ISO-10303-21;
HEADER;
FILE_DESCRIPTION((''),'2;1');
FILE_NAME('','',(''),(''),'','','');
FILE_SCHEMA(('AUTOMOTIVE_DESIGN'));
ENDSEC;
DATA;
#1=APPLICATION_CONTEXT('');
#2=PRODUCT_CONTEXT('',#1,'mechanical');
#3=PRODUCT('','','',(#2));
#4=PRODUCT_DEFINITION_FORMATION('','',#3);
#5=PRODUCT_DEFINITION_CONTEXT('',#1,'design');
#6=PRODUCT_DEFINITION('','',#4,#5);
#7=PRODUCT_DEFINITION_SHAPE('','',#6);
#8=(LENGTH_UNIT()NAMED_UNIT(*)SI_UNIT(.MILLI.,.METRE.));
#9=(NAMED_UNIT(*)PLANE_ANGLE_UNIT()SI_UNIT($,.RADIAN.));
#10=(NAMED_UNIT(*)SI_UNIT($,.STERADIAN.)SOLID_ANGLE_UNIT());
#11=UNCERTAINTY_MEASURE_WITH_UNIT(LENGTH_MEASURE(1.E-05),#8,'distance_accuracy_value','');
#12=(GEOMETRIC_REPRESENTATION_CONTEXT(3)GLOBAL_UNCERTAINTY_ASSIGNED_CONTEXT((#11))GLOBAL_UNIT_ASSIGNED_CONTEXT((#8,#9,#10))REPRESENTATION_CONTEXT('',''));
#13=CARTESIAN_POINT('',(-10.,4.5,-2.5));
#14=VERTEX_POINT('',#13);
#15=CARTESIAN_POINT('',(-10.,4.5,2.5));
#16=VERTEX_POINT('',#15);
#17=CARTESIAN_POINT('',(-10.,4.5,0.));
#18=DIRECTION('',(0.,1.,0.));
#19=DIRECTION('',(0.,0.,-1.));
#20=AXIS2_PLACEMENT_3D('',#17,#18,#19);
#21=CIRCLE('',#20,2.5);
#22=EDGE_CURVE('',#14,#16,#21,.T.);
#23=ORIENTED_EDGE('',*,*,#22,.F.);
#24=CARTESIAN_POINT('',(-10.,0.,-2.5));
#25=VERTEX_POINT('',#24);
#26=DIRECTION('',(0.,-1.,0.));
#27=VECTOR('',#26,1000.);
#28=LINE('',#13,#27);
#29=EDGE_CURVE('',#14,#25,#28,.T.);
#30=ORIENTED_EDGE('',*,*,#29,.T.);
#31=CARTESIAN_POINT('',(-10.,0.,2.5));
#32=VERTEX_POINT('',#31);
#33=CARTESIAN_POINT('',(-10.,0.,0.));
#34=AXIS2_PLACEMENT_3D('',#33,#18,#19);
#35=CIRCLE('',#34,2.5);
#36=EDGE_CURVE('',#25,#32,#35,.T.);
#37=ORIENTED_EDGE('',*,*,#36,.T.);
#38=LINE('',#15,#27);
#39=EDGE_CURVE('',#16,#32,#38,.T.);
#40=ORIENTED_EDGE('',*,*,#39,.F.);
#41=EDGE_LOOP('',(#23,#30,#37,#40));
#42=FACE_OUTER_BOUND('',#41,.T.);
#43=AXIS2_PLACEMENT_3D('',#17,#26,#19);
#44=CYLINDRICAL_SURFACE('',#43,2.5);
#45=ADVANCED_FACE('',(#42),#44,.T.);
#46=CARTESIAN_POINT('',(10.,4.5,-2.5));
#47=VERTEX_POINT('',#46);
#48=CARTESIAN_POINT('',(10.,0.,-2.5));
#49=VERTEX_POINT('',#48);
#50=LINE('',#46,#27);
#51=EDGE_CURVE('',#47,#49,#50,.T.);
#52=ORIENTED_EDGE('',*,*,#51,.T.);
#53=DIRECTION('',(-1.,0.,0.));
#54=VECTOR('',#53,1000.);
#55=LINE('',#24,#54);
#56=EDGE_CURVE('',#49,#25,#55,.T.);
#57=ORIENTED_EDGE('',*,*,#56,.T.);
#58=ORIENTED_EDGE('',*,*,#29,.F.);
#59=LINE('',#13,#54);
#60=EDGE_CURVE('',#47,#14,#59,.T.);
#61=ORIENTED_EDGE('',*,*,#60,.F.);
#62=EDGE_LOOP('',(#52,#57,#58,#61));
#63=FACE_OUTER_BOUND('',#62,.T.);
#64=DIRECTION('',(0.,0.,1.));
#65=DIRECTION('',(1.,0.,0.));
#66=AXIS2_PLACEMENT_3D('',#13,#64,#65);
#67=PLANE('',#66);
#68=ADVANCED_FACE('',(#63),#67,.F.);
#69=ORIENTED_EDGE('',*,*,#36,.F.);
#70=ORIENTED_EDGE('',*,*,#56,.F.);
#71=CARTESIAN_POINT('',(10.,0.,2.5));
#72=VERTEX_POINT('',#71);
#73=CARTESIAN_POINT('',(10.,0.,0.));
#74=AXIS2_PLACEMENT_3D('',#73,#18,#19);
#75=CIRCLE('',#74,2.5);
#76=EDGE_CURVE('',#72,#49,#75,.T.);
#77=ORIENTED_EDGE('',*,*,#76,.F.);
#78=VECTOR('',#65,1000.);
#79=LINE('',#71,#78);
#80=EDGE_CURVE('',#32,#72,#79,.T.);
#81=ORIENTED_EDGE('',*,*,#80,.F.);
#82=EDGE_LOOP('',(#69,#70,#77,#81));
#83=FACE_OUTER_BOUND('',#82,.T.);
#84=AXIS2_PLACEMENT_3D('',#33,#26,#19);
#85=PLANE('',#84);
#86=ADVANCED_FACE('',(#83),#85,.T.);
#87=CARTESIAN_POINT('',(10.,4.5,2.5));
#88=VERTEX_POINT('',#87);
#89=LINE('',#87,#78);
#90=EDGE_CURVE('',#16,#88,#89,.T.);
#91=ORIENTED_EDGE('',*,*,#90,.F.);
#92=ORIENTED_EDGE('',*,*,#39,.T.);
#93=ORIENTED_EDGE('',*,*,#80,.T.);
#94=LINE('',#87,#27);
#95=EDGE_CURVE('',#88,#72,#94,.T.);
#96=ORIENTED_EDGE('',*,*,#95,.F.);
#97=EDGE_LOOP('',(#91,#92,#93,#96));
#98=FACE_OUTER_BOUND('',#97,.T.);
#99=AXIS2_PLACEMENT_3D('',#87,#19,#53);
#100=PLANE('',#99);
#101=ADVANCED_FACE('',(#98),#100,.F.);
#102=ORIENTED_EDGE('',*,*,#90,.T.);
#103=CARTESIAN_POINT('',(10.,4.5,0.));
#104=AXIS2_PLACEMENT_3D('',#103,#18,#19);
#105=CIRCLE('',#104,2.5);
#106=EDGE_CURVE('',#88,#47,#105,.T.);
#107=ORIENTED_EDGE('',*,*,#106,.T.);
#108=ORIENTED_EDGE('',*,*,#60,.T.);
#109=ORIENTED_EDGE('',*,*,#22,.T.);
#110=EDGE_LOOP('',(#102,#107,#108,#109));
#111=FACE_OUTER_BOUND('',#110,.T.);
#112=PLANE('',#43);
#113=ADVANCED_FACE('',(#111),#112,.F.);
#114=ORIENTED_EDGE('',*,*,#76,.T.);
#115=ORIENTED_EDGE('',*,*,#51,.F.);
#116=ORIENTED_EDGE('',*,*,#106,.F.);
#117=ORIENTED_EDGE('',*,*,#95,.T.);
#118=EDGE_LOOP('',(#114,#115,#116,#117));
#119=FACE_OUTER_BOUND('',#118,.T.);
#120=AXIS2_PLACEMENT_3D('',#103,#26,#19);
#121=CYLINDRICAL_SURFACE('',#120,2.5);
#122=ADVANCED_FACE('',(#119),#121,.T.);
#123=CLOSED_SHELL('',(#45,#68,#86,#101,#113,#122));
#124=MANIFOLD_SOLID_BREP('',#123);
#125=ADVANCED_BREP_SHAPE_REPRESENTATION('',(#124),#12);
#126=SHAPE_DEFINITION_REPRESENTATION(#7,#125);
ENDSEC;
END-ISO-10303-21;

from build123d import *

# Parameters (mm, degrees)
BOSS_EXTRUDE1_DEPTH = 4.5


with BuildPart() as part:
    # Sketch1 → Boss-Extrude1 (new body)
    with BuildSketch(Plane(origin=(0, 0, 0), x_dir=(1, 0, 0), z_dir=(0, 1, 0))):
        with BuildLine():
            Line((-10, 2.5), (10, 2.5))
            ThreePointArc((10, 2.5), (12.5, 0), (10, -2.5))
            Line((10, -2.5), (-10, -2.5))
            ThreePointArc((-10, -2.5), (-12.5, 0), (-10, 2.5))
        make_face()
    extrude(amount=BOSS_EXTRUDE1_DEPTH)


solid = part.part
